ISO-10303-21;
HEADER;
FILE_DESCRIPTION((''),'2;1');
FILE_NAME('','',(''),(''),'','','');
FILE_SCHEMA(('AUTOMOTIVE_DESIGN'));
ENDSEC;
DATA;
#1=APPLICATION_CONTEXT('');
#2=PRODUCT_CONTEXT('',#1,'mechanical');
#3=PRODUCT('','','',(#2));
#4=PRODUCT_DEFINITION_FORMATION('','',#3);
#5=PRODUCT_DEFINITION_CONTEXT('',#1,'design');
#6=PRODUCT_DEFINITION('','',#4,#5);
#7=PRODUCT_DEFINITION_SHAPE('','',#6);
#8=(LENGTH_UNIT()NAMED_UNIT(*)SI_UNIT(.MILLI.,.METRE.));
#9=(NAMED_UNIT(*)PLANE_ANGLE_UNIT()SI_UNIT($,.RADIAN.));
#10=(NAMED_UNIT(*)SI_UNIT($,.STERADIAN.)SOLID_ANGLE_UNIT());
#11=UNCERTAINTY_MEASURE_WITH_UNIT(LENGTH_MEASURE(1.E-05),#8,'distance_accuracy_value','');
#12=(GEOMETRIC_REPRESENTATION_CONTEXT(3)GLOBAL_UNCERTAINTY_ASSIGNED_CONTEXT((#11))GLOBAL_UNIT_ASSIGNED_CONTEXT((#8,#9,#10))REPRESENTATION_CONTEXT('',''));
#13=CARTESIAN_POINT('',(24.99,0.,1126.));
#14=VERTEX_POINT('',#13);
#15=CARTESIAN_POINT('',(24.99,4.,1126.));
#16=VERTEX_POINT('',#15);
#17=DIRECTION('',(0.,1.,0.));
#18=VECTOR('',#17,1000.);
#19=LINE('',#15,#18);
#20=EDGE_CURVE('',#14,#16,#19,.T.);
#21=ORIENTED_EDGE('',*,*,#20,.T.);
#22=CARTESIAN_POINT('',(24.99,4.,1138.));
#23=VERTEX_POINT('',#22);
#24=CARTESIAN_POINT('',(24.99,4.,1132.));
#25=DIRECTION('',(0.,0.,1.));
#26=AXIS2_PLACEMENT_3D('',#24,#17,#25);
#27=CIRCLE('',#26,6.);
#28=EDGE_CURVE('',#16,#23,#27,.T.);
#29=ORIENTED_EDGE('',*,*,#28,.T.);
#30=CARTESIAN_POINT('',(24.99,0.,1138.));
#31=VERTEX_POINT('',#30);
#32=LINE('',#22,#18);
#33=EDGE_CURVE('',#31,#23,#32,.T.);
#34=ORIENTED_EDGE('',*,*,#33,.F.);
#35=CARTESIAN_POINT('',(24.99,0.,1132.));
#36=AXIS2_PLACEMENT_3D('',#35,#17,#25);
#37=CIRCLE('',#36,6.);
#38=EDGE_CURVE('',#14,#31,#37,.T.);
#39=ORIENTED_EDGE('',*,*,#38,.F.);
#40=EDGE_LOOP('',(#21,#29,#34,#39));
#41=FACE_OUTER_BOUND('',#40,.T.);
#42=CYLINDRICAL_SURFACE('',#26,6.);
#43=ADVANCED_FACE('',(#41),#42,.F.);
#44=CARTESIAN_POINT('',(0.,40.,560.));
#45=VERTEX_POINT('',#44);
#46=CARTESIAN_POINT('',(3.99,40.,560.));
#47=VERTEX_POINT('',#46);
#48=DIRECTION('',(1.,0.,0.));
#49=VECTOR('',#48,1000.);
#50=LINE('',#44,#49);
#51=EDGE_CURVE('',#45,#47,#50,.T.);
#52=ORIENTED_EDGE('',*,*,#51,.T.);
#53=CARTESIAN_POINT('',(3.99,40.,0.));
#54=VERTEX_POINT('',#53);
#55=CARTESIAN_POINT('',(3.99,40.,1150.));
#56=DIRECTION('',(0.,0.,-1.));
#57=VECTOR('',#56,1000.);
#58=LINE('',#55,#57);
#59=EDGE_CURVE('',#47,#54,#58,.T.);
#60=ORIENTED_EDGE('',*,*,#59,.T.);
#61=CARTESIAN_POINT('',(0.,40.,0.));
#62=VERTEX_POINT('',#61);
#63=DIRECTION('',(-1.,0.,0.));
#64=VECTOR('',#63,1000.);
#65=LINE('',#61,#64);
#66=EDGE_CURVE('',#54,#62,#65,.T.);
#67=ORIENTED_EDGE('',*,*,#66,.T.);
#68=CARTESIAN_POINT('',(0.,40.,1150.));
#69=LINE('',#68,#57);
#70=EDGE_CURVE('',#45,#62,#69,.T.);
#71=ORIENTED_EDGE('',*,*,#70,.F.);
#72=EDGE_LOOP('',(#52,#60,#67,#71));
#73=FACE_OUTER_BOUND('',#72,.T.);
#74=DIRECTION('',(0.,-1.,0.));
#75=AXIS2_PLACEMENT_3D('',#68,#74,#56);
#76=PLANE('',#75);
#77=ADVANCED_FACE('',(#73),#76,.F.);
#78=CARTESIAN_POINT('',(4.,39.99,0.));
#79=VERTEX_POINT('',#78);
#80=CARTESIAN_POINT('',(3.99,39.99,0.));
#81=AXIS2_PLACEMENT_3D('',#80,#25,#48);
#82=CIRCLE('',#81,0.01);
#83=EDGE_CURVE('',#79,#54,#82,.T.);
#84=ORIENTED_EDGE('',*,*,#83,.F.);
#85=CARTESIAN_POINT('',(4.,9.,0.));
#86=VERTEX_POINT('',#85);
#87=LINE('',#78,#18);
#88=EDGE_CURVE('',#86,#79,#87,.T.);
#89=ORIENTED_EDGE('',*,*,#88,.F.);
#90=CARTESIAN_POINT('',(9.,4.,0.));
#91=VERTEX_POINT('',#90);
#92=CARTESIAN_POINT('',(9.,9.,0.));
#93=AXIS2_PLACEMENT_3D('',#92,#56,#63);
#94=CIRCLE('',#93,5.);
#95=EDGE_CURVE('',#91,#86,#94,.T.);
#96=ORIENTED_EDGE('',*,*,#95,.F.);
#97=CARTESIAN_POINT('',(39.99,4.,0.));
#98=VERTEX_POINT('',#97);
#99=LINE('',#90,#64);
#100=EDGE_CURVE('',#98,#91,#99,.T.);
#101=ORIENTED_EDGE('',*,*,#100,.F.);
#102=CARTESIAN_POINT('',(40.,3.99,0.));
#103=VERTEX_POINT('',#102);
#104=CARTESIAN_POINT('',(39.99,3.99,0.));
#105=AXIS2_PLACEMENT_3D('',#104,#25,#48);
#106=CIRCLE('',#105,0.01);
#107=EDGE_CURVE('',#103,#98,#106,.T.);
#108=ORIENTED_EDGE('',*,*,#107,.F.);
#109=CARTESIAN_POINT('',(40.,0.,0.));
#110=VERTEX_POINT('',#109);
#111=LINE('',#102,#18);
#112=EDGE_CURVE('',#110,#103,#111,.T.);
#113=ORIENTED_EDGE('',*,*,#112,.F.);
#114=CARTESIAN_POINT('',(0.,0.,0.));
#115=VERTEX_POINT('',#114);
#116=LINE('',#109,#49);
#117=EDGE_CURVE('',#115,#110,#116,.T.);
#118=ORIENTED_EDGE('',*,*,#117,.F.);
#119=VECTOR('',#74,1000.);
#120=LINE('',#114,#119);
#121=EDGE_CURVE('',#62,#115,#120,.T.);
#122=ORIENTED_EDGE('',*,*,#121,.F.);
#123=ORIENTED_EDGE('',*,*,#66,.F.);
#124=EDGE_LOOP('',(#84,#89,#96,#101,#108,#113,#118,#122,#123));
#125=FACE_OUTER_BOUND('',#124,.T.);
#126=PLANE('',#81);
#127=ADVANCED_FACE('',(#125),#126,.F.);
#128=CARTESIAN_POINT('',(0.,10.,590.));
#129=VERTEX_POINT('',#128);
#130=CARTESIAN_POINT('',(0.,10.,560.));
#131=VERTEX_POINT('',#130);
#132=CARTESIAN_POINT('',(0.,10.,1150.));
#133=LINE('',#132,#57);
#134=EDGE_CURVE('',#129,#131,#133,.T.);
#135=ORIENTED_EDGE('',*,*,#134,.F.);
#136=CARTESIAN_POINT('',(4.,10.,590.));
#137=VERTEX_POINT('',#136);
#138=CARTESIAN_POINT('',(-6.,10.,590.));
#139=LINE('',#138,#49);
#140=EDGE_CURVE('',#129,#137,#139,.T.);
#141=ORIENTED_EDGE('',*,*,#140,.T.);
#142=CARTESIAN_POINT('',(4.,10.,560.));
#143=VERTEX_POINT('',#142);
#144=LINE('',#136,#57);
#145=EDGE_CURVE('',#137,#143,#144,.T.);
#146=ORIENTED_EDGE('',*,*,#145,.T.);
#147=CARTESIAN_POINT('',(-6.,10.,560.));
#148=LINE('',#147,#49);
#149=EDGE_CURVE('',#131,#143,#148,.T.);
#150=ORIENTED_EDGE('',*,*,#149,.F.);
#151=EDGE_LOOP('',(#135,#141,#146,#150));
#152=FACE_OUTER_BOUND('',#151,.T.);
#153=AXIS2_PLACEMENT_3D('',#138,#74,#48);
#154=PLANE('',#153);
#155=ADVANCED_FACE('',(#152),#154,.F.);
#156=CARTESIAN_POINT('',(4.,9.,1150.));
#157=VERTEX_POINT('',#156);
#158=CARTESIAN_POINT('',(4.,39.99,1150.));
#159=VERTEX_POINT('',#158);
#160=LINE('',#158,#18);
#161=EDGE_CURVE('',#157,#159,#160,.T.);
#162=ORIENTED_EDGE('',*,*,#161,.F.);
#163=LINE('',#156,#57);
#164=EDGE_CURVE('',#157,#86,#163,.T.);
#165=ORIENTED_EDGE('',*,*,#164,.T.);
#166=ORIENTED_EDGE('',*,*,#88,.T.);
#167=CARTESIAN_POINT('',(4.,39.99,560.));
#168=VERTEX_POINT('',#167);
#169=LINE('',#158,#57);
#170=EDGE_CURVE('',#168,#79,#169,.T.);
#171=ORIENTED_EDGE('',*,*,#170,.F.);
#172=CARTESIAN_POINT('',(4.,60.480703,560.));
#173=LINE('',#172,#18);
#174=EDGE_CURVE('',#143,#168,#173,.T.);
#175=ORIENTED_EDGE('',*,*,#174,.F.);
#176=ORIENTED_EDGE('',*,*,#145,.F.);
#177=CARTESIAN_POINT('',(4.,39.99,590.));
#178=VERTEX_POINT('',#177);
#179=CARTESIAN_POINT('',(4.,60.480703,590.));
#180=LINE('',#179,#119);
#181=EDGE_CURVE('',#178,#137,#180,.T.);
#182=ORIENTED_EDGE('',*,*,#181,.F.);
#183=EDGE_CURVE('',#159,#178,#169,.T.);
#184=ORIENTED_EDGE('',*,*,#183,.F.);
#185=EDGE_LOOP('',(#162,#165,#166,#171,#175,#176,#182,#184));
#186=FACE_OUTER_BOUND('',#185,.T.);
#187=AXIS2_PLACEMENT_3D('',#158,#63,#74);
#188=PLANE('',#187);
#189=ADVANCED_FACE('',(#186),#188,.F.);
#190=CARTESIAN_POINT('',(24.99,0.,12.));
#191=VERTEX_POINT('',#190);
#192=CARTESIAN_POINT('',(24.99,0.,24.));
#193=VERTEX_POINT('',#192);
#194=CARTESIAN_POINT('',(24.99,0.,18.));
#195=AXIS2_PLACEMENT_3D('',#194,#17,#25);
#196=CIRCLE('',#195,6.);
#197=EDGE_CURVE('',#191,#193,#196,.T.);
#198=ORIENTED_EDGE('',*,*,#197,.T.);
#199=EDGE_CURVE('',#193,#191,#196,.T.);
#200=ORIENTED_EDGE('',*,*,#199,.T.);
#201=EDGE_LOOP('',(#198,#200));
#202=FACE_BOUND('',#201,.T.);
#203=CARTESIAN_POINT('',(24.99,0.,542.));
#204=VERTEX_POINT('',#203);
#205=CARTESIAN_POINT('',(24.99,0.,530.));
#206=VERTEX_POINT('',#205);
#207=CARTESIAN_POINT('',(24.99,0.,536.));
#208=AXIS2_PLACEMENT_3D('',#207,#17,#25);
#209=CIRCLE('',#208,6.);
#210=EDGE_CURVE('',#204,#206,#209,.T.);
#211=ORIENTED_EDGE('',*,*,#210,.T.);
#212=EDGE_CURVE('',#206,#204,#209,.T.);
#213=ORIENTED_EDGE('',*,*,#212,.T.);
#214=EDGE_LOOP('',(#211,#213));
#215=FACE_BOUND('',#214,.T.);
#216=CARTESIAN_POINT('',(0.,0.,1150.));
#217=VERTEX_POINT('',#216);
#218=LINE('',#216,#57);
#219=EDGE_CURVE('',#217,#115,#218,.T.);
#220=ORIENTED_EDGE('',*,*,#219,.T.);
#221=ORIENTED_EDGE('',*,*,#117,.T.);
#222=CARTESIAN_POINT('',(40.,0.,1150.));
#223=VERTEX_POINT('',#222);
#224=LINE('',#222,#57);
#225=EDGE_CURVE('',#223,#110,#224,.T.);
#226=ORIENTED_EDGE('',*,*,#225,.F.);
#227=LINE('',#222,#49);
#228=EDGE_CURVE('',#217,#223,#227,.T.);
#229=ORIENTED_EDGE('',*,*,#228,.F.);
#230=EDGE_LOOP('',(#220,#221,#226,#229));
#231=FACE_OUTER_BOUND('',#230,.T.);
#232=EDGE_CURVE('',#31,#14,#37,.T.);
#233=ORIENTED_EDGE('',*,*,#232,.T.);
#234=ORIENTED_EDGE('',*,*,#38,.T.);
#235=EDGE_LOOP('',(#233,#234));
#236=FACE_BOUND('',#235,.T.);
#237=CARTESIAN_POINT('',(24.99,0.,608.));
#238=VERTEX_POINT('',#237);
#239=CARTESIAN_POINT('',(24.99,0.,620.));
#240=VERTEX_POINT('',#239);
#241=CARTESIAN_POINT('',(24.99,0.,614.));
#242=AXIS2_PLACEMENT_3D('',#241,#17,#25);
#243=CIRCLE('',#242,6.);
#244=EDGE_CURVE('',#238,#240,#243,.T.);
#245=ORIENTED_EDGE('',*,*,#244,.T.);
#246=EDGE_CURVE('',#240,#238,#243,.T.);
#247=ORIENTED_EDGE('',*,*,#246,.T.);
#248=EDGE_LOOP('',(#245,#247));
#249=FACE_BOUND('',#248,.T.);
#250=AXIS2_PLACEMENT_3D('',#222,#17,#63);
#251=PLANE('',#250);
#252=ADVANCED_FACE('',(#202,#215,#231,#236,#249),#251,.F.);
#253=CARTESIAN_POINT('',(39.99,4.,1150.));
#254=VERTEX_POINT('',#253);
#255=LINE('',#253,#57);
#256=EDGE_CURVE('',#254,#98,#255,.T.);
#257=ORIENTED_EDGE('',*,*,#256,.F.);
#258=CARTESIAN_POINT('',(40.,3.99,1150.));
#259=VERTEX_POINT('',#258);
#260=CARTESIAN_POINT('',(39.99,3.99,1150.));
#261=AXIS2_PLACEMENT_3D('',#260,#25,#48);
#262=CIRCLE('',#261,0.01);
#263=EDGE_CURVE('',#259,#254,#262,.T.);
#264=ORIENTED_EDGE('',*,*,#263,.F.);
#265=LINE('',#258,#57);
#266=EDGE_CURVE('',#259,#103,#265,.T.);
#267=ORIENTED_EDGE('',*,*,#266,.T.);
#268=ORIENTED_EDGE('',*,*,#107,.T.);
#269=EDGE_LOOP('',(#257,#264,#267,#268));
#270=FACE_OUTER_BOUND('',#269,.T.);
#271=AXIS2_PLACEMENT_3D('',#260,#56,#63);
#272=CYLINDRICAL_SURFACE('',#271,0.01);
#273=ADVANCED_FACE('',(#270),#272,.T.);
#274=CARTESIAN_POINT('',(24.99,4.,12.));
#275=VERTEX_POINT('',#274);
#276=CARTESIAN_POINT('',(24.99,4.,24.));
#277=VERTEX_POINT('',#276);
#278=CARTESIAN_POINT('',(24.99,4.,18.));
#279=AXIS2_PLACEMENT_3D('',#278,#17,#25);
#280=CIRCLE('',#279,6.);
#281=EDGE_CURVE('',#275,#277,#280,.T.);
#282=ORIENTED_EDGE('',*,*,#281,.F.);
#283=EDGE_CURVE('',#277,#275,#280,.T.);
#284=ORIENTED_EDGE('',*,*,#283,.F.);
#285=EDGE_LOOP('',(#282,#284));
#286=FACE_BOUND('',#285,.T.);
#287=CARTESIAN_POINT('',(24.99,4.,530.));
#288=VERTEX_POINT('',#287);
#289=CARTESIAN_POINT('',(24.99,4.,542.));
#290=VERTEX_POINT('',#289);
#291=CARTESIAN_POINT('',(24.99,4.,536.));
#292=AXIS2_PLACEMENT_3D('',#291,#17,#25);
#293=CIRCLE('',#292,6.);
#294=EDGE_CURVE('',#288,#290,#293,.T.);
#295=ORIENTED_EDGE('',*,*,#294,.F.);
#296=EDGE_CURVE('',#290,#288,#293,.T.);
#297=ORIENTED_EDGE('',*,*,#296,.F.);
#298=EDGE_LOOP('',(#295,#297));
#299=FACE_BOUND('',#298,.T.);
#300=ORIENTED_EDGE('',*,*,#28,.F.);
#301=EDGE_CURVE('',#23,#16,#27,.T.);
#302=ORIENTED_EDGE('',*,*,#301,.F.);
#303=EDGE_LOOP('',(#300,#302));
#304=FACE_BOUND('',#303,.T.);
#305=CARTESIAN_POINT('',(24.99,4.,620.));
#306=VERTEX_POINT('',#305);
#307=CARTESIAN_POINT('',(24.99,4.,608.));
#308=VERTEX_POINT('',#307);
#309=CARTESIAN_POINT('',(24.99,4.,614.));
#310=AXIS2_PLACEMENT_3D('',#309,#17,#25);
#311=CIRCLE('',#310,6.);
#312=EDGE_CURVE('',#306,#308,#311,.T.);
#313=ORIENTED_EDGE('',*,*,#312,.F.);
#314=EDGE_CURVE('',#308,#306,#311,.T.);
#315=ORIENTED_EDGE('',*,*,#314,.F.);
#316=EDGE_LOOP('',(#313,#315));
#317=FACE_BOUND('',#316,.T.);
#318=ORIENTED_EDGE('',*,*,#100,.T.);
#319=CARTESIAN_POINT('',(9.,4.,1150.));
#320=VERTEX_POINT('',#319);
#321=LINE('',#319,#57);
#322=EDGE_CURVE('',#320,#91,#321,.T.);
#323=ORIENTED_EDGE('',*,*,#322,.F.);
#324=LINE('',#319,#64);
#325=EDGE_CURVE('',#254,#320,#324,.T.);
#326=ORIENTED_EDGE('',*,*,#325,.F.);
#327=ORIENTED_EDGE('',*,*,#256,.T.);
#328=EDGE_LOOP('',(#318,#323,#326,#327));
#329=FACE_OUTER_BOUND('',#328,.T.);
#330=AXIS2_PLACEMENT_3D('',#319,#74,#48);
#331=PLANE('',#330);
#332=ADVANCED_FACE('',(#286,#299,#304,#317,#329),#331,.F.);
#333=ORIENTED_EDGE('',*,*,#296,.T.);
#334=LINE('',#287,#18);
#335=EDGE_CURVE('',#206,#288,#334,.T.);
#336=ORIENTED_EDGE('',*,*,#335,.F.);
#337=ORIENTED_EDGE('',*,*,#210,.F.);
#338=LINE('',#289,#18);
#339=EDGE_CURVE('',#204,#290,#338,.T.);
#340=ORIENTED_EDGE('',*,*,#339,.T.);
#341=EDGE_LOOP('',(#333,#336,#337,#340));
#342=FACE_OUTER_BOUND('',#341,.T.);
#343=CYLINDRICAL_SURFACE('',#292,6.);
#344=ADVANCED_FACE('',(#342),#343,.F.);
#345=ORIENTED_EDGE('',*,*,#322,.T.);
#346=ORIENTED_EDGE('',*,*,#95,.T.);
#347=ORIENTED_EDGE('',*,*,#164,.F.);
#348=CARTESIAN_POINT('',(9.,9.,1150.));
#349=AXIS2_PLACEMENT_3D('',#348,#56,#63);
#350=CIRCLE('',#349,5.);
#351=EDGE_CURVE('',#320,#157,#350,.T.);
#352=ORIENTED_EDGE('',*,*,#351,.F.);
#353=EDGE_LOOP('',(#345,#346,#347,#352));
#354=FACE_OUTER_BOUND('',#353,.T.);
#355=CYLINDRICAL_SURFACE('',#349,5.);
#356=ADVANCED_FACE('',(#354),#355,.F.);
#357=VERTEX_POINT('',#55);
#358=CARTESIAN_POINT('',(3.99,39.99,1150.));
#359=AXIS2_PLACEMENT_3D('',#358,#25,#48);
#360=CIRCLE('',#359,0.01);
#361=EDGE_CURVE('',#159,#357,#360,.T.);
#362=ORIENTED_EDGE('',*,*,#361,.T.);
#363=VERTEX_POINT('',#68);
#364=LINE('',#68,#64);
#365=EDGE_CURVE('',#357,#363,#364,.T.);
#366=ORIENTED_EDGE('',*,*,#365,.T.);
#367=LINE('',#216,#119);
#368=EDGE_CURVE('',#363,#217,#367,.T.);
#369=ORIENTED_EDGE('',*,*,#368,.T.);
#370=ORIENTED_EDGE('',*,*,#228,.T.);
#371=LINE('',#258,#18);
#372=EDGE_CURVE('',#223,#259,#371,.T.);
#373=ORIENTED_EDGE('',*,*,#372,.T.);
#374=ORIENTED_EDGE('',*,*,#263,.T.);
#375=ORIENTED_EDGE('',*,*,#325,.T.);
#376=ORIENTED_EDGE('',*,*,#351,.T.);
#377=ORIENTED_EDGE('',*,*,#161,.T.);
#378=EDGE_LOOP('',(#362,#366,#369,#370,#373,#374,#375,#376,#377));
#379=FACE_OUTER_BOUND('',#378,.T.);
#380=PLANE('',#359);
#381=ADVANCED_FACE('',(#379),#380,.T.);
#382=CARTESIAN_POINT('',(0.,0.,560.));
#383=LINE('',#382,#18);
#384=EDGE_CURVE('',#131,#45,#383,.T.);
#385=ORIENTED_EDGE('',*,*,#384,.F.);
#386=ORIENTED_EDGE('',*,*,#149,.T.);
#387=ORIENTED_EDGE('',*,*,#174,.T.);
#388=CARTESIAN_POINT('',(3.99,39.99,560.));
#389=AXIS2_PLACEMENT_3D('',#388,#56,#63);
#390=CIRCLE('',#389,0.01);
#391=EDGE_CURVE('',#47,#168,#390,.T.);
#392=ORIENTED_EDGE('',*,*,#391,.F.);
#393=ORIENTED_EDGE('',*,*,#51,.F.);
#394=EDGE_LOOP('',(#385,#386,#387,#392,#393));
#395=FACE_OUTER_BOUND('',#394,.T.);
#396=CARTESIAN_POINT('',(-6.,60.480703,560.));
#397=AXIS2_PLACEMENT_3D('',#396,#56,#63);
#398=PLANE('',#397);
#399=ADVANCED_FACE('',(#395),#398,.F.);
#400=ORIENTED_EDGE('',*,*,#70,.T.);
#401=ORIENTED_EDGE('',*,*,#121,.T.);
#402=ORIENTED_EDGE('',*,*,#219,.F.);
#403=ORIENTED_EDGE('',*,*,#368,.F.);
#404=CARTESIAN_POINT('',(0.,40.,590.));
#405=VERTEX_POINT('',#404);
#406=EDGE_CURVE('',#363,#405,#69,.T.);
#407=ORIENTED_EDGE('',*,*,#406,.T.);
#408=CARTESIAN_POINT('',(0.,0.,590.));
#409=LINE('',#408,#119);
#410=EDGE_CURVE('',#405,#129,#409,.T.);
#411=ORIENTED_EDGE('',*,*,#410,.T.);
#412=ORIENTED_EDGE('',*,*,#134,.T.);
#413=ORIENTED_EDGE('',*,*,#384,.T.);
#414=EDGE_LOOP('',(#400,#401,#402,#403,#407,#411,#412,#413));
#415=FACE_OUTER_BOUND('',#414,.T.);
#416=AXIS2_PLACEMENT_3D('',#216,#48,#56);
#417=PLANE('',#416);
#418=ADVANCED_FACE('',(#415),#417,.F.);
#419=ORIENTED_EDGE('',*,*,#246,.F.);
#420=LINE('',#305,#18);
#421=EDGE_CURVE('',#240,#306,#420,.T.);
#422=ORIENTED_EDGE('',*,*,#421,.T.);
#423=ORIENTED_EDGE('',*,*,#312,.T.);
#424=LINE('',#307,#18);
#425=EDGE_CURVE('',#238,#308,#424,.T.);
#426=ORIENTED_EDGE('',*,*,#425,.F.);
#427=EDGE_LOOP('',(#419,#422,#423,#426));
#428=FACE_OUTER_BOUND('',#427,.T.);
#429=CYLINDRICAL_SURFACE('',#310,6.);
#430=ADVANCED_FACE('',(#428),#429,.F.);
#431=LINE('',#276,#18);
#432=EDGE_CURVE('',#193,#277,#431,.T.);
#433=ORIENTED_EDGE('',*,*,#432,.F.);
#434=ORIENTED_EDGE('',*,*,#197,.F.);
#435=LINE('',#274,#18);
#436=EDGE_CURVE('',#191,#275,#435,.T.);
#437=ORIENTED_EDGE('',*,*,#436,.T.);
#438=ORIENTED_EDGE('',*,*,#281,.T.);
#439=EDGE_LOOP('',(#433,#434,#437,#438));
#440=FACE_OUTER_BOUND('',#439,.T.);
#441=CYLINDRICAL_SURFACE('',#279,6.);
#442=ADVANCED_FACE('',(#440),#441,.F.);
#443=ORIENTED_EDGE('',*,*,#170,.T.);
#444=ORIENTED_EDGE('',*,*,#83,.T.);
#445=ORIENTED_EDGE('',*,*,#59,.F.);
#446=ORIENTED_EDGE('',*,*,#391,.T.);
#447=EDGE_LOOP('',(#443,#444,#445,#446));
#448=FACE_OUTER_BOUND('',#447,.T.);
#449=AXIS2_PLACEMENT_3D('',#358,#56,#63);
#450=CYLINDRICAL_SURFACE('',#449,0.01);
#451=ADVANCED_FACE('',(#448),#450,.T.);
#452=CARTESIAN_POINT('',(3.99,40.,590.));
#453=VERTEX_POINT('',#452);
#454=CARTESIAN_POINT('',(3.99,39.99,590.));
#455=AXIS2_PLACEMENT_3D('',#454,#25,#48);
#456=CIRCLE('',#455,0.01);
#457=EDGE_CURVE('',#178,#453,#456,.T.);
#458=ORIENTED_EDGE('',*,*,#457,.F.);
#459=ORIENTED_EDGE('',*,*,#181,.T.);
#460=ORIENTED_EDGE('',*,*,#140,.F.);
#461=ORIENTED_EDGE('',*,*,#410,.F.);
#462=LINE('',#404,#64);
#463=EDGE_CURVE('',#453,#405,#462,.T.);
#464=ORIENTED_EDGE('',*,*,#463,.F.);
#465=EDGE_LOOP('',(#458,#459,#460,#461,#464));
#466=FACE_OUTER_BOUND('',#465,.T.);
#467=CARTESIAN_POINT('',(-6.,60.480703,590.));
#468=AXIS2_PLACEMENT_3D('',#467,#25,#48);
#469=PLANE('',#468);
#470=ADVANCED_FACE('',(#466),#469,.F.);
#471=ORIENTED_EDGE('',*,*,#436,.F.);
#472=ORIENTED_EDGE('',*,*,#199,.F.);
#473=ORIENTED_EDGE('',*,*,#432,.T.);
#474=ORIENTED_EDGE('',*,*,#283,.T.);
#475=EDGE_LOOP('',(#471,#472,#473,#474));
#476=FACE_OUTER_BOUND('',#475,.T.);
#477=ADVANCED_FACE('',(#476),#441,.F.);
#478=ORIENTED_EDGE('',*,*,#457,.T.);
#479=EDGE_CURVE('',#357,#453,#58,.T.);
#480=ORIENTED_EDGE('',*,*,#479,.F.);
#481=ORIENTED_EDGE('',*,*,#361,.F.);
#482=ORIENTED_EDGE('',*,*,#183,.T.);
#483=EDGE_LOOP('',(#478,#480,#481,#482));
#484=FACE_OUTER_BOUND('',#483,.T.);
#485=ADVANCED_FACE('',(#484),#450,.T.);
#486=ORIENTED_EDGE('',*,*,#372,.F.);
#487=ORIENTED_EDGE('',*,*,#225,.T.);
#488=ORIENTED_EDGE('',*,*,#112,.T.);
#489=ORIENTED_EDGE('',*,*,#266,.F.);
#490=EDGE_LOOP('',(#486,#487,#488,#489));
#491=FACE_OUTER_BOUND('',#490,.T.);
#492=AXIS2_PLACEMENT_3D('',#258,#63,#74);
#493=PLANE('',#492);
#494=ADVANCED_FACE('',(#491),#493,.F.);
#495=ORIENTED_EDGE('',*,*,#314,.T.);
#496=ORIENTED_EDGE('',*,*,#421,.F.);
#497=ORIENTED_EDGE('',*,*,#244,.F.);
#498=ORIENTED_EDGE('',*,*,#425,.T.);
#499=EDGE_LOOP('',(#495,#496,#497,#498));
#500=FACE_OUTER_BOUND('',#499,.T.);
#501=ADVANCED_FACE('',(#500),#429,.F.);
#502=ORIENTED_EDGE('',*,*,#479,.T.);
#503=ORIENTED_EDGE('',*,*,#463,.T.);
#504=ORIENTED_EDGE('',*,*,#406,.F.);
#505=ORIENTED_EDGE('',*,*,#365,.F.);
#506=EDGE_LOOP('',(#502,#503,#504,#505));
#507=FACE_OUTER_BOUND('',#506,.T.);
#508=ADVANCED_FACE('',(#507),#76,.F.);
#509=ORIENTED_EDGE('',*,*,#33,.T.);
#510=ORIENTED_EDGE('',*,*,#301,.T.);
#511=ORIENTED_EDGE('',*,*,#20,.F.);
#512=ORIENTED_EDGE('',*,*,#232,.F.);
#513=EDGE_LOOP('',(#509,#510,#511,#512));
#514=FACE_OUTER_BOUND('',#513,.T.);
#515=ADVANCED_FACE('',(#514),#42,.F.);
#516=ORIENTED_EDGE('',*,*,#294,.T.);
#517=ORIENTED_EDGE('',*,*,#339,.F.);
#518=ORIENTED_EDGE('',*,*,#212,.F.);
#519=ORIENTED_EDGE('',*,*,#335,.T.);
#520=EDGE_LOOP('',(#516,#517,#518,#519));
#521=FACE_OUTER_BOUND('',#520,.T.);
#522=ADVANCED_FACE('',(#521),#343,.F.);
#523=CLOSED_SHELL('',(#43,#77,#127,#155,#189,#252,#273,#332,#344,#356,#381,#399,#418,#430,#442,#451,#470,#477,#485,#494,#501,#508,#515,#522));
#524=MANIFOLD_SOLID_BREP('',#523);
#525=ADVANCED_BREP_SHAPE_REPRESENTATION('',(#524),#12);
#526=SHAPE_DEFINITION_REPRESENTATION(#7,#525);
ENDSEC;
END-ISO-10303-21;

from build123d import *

# Parameters (mm, degrees)
EXTRUDE_1_DEPTH         = 1150
HOLE_WIZARD_12_0_12_1_D = 12
SKETCH_4_W              = 30
SKETCH_4_H              = 50.480703337
CUT_EXTRUDE_1_DEPTH     = 10


with BuildPart() as part:
    # 草图1 → 拉伸1 (new body)
    with BuildSketch(Plane.XY):
        with BuildLine():
            Line((0, 0), (0, 40))
            Line((0, 40), (3.99, 40))
            ThreePointArc((3.99, 40), (3.997071068, 39.997071068), (4, 39.99))
            Line((4, 39.99), (4, 9))
            ThreePointArc((4, 9), (5.464466094, 5.464466094), (9, 4))
            Line((9, 4), (39.99, 4))
            ThreePointArc((39.99, 4), (39.997071068, 3.997071068), (40, 3.99))
            Line((40, 3.99), (40, 0))
            Line((40, 0), (0, 0))
        make_face()
    extrude(amount=EXTRUDE_1_DEPTH)

    # Ø12.0 (12) 直径孔1 (through all)
    with Locations(Plane(origin=(0, 4, 0), x_dir=(1, 0, 0), z_dir=(0, 1, 0))):
        with Locations((24.99, -1132), (24.99, -614), (24.99, -536), (24.99, -18)):
            Hole(HOLE_WIZARD_12_0_12_1_D / 2)

    # 草图4 → 切除-拉伸1 (cut)
    with BuildSketch(Plane(origin=(4, 0, 0), x_dir=(0, 0, -1), z_dir=(1, 0, 0))):
        with Locations((-575, 35.240351668)):
            Rectangle(SKETCH_4_W, SKETCH_4_H)
    extrude(amount=-CUT_EXTRUDE_1_DEPTH, mode=Mode.SUBTRACT)


solid = part.part
